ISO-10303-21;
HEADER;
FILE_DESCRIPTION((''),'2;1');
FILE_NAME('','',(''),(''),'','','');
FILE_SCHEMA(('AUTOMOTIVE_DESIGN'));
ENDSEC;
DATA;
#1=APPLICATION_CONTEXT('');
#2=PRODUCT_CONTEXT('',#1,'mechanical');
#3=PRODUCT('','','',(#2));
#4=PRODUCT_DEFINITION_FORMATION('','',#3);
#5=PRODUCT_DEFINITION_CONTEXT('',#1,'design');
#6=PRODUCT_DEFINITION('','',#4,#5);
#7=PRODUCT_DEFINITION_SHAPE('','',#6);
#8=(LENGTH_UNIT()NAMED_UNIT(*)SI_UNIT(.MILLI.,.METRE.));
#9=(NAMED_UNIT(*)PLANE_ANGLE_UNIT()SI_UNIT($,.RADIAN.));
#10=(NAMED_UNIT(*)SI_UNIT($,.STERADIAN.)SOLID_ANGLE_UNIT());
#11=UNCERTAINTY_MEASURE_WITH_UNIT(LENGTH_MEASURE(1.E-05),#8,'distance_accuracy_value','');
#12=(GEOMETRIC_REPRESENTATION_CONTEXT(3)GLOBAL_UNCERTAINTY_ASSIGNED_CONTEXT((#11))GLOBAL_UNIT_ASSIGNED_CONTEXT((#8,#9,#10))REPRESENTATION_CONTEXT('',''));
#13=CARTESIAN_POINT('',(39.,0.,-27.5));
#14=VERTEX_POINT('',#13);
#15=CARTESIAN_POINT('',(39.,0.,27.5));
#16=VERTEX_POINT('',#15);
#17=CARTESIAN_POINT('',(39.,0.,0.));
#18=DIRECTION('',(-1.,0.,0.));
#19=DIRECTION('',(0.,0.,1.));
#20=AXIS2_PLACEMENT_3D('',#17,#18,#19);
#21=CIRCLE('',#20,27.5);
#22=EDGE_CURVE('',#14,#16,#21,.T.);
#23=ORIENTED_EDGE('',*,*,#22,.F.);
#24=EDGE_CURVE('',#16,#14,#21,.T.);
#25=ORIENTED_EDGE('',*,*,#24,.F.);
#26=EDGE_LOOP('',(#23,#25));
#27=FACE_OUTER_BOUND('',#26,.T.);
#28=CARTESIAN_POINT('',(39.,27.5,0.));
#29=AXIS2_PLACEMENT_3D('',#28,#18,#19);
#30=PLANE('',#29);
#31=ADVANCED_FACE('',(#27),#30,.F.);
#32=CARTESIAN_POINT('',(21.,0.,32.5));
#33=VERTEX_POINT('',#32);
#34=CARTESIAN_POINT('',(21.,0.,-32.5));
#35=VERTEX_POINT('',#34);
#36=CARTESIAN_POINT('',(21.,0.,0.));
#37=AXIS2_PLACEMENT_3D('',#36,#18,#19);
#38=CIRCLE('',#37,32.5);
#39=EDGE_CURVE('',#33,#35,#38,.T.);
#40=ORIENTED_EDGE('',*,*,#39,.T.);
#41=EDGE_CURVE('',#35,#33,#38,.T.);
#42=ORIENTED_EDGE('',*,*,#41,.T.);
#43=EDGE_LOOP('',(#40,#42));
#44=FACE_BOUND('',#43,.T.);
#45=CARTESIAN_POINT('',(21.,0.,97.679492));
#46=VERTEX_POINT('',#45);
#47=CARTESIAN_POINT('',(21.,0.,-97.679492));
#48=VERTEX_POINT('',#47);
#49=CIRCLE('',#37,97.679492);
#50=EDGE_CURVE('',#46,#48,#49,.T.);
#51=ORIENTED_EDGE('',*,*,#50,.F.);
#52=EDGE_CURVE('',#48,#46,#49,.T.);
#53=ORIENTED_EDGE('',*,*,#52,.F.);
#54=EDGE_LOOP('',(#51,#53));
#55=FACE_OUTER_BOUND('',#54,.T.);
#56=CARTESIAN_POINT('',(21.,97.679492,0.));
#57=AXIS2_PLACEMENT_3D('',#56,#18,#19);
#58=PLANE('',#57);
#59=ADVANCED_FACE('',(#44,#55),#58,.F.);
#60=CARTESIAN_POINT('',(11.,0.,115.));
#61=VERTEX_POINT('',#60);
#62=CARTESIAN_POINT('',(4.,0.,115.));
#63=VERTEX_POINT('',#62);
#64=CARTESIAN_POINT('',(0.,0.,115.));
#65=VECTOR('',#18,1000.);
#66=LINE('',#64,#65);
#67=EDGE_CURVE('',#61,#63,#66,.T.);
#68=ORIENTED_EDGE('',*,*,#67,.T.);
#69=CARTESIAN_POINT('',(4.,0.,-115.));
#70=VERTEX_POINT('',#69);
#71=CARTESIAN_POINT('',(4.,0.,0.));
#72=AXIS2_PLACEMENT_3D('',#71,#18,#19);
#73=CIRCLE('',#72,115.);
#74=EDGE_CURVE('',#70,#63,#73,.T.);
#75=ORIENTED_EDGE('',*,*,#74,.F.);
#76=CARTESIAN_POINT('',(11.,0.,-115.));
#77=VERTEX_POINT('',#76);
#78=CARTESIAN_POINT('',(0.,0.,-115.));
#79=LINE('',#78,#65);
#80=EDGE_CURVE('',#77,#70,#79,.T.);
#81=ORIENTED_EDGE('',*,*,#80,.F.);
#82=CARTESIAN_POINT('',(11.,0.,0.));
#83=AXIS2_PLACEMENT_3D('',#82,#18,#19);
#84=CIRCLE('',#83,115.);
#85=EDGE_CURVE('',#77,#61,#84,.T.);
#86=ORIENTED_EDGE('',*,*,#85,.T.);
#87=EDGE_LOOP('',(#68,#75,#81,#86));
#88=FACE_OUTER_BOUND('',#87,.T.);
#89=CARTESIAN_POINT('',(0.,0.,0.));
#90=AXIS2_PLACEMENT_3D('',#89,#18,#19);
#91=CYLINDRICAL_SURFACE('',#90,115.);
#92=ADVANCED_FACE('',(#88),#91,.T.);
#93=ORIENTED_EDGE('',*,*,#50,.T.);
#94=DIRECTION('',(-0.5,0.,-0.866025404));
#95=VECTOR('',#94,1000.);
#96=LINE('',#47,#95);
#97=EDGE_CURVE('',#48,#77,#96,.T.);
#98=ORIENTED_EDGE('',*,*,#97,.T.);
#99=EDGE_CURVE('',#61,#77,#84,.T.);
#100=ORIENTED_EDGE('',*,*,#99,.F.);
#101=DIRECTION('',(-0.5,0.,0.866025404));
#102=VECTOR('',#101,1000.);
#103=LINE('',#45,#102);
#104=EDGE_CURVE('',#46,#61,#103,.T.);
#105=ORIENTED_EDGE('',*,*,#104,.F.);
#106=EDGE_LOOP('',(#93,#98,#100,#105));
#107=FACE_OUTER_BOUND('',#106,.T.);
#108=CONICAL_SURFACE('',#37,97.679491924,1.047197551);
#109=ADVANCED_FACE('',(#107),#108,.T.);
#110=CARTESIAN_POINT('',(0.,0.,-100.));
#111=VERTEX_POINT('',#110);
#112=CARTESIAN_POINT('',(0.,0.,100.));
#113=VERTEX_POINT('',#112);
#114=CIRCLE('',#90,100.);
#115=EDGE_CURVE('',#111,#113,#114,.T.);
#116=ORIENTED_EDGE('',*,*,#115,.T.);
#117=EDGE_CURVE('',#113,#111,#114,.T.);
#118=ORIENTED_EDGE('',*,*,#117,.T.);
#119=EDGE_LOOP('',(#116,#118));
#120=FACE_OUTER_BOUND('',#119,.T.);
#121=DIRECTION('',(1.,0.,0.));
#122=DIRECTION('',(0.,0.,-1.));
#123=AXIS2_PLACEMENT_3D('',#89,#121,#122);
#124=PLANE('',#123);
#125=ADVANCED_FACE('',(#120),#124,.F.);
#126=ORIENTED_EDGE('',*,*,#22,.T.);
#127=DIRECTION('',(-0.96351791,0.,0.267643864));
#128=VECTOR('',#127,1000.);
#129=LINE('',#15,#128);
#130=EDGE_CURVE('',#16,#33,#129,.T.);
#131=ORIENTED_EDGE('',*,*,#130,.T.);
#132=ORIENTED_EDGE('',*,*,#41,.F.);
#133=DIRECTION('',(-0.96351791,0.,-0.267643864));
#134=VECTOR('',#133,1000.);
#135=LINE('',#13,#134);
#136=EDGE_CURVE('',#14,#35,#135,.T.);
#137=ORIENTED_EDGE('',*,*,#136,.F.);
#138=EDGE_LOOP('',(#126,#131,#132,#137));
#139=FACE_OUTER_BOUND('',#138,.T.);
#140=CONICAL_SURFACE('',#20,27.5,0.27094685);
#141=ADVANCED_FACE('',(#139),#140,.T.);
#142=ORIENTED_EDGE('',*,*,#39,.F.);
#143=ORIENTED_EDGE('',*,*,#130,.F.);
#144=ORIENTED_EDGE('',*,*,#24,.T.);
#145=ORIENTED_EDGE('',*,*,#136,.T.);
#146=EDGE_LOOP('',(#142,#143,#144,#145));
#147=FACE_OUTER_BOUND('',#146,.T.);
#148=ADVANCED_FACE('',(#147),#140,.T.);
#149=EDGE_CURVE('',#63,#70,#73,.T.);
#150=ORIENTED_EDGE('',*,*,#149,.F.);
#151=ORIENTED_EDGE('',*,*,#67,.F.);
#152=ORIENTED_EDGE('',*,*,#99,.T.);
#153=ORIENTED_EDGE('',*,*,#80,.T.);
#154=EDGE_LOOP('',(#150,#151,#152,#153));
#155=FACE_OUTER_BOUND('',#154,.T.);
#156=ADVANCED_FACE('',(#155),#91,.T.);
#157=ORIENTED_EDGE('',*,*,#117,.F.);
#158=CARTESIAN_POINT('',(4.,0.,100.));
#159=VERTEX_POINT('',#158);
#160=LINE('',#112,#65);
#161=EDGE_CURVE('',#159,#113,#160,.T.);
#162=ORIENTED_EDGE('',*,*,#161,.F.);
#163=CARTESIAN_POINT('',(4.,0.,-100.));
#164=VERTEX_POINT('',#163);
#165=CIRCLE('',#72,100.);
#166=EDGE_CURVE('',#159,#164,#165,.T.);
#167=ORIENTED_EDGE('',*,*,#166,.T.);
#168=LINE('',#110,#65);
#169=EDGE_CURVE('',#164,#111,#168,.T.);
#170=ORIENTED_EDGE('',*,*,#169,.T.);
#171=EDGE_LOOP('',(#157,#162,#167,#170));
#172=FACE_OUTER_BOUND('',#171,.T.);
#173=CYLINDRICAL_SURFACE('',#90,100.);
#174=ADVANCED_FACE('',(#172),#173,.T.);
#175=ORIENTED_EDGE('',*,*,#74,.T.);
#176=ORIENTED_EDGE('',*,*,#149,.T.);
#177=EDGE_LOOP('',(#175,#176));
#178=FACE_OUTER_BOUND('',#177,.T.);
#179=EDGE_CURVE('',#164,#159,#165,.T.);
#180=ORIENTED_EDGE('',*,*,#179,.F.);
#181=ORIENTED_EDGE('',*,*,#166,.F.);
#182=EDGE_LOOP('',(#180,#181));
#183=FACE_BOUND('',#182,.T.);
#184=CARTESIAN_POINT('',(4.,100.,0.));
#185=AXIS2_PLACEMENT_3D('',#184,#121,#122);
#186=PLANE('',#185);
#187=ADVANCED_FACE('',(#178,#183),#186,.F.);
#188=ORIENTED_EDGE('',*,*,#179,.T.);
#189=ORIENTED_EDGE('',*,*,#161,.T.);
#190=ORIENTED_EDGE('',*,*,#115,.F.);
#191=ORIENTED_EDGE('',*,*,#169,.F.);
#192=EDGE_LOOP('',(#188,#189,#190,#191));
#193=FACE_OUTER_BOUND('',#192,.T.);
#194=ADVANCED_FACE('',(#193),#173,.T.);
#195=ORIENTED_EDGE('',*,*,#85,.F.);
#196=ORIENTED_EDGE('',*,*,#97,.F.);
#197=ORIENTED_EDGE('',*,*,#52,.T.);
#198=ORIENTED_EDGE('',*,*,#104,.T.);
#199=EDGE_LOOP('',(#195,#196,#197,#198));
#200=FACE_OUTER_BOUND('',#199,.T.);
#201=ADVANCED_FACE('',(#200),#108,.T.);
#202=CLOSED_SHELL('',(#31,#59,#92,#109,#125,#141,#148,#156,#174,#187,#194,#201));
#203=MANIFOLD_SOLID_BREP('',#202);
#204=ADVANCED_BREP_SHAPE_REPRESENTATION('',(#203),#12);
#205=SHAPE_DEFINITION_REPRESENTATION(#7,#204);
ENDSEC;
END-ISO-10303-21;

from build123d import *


with BuildPart() as part:
    # Sketch1 → Revolve1 (revolve)
    with BuildSketch(Plane.XY, mode=Mode.PRIVATE) as revolve1_sk:
        Polygon((0, 0), (0, 100), (4, 100), (4, 115), (11, 115), (21, 97.679491924), (21, 32.5), (39, 27.5), (39, 0), align=None)
    revolve(revolve1_sk.sketch.rotate(Axis((0, 0, 0), (1, 0, 0)), 90), axis=Axis((0, 0, 0), (1, 0, 0)))


solid = part.part
